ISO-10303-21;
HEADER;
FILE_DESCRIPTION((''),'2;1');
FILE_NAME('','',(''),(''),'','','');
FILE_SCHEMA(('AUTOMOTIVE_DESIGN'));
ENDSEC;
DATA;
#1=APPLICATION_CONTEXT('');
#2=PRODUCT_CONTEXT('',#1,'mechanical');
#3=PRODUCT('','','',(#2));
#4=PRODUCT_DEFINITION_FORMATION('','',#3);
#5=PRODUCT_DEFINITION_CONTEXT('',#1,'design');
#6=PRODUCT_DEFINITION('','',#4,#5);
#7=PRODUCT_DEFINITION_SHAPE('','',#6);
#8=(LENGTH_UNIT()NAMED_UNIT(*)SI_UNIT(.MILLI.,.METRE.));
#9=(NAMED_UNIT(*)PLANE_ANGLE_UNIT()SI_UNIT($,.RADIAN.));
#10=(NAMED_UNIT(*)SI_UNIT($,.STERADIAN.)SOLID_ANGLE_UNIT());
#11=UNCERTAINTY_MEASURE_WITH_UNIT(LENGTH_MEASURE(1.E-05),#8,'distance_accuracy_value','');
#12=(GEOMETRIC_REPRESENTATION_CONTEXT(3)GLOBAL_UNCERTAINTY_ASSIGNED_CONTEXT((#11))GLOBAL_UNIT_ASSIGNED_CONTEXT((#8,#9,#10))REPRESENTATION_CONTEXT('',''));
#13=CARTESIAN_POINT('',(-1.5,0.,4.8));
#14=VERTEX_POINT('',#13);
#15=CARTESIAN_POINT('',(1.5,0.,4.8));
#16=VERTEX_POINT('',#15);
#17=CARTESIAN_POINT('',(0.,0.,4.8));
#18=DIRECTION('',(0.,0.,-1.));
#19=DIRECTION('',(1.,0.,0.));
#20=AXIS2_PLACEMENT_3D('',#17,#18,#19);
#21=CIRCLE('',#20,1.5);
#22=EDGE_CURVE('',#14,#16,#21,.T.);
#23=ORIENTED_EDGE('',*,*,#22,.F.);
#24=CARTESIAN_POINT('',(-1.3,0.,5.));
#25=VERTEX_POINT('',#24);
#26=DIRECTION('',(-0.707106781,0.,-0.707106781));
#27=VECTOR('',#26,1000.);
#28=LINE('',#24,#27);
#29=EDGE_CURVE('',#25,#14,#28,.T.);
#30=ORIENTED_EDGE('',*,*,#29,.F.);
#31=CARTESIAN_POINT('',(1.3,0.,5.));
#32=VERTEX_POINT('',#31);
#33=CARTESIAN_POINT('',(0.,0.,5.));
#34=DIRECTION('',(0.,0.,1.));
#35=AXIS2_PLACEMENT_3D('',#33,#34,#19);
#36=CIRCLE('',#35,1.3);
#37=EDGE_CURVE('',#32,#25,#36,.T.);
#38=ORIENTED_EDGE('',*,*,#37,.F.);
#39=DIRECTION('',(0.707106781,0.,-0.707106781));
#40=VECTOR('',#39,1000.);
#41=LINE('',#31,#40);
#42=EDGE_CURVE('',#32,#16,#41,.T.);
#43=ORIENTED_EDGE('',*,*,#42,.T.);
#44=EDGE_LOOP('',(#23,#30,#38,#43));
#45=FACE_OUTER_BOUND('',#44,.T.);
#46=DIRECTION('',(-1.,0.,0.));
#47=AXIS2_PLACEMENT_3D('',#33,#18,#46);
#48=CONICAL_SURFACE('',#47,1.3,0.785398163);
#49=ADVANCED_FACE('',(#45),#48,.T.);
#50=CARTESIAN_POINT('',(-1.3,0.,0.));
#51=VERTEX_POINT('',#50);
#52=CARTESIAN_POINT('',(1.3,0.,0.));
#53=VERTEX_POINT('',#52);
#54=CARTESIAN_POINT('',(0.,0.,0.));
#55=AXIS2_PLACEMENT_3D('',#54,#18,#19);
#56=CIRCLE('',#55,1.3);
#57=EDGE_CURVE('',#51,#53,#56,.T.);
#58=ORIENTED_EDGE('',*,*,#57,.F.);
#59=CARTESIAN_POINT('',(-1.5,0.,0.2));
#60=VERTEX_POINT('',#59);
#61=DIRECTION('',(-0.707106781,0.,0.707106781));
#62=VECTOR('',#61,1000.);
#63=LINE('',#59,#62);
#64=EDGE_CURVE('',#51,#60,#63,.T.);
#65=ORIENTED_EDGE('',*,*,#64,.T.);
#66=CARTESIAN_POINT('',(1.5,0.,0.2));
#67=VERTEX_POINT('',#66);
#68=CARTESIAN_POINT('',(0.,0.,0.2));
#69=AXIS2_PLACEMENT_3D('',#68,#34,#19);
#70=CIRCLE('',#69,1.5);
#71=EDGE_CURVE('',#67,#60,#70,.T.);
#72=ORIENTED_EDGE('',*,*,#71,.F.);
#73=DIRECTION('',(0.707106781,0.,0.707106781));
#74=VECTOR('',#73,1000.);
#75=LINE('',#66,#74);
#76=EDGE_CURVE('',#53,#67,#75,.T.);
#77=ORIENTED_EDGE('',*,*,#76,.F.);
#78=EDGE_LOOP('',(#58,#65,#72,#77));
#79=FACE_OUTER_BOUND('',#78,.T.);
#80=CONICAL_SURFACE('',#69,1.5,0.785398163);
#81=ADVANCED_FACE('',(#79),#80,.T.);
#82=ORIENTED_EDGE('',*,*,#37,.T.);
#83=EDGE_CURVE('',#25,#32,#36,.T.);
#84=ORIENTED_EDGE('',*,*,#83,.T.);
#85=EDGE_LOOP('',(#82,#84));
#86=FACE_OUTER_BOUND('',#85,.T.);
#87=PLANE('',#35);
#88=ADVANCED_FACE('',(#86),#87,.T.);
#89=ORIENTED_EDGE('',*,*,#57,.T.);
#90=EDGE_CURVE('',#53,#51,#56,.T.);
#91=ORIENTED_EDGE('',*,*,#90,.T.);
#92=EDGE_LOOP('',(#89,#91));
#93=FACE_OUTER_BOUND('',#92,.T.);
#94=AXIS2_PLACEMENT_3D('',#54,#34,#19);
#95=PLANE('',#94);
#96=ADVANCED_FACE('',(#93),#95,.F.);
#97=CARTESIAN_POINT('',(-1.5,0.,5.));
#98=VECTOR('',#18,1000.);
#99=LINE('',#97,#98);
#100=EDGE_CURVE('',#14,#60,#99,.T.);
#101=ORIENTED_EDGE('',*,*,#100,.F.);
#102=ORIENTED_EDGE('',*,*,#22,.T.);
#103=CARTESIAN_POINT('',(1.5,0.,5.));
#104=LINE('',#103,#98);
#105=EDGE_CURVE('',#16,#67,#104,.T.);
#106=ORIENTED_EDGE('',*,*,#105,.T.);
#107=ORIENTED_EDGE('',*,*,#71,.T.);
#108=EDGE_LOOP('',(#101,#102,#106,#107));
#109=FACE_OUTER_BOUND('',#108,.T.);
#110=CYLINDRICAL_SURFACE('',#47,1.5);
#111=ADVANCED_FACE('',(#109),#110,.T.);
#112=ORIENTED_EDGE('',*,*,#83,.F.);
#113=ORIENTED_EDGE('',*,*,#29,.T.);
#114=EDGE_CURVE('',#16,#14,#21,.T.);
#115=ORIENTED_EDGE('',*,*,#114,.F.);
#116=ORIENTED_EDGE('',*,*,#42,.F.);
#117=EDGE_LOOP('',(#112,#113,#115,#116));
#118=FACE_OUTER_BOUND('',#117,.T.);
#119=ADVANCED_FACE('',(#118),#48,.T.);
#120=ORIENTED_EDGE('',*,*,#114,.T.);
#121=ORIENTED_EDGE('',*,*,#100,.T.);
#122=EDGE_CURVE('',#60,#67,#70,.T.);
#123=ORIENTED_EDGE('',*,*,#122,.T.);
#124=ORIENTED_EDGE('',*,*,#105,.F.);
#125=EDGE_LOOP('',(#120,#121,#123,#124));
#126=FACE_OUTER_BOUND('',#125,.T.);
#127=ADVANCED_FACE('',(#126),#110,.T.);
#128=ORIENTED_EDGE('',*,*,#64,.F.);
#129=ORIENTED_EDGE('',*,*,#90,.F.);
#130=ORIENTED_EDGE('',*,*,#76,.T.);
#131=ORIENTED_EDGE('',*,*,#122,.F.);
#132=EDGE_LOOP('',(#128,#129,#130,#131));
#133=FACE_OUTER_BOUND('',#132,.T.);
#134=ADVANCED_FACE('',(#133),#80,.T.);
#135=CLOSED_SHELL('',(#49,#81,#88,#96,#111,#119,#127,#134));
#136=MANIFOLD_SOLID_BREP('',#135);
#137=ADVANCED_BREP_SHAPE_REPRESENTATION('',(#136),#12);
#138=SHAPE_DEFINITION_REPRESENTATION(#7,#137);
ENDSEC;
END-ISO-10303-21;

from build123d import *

# Parameters (mm, degrees)
SKETCH1_R           = 1.5
BOSS_EXTRUDE1_DEPTH = 5
CHAMFER1_SIZE       = 0.2


with BuildPart() as part:
    # Sketch1 → Boss-Extrude1 (new body)
    with BuildSketch(Plane.XY):
        Circle(SKETCH1_R)
    extrude(amount=BOSS_EXTRUDE1_DEPTH)

    # Chamfer1
    chamfer1_edges = [part.edges().sort_by_distance(p)[0] for p in [
        (-1.5, 0, 0),
        (-1.5, 0, 5),
    ]]
    chamfer(chamfer1_edges, length=CHAMFER1_SIZE)


solid = part.part
